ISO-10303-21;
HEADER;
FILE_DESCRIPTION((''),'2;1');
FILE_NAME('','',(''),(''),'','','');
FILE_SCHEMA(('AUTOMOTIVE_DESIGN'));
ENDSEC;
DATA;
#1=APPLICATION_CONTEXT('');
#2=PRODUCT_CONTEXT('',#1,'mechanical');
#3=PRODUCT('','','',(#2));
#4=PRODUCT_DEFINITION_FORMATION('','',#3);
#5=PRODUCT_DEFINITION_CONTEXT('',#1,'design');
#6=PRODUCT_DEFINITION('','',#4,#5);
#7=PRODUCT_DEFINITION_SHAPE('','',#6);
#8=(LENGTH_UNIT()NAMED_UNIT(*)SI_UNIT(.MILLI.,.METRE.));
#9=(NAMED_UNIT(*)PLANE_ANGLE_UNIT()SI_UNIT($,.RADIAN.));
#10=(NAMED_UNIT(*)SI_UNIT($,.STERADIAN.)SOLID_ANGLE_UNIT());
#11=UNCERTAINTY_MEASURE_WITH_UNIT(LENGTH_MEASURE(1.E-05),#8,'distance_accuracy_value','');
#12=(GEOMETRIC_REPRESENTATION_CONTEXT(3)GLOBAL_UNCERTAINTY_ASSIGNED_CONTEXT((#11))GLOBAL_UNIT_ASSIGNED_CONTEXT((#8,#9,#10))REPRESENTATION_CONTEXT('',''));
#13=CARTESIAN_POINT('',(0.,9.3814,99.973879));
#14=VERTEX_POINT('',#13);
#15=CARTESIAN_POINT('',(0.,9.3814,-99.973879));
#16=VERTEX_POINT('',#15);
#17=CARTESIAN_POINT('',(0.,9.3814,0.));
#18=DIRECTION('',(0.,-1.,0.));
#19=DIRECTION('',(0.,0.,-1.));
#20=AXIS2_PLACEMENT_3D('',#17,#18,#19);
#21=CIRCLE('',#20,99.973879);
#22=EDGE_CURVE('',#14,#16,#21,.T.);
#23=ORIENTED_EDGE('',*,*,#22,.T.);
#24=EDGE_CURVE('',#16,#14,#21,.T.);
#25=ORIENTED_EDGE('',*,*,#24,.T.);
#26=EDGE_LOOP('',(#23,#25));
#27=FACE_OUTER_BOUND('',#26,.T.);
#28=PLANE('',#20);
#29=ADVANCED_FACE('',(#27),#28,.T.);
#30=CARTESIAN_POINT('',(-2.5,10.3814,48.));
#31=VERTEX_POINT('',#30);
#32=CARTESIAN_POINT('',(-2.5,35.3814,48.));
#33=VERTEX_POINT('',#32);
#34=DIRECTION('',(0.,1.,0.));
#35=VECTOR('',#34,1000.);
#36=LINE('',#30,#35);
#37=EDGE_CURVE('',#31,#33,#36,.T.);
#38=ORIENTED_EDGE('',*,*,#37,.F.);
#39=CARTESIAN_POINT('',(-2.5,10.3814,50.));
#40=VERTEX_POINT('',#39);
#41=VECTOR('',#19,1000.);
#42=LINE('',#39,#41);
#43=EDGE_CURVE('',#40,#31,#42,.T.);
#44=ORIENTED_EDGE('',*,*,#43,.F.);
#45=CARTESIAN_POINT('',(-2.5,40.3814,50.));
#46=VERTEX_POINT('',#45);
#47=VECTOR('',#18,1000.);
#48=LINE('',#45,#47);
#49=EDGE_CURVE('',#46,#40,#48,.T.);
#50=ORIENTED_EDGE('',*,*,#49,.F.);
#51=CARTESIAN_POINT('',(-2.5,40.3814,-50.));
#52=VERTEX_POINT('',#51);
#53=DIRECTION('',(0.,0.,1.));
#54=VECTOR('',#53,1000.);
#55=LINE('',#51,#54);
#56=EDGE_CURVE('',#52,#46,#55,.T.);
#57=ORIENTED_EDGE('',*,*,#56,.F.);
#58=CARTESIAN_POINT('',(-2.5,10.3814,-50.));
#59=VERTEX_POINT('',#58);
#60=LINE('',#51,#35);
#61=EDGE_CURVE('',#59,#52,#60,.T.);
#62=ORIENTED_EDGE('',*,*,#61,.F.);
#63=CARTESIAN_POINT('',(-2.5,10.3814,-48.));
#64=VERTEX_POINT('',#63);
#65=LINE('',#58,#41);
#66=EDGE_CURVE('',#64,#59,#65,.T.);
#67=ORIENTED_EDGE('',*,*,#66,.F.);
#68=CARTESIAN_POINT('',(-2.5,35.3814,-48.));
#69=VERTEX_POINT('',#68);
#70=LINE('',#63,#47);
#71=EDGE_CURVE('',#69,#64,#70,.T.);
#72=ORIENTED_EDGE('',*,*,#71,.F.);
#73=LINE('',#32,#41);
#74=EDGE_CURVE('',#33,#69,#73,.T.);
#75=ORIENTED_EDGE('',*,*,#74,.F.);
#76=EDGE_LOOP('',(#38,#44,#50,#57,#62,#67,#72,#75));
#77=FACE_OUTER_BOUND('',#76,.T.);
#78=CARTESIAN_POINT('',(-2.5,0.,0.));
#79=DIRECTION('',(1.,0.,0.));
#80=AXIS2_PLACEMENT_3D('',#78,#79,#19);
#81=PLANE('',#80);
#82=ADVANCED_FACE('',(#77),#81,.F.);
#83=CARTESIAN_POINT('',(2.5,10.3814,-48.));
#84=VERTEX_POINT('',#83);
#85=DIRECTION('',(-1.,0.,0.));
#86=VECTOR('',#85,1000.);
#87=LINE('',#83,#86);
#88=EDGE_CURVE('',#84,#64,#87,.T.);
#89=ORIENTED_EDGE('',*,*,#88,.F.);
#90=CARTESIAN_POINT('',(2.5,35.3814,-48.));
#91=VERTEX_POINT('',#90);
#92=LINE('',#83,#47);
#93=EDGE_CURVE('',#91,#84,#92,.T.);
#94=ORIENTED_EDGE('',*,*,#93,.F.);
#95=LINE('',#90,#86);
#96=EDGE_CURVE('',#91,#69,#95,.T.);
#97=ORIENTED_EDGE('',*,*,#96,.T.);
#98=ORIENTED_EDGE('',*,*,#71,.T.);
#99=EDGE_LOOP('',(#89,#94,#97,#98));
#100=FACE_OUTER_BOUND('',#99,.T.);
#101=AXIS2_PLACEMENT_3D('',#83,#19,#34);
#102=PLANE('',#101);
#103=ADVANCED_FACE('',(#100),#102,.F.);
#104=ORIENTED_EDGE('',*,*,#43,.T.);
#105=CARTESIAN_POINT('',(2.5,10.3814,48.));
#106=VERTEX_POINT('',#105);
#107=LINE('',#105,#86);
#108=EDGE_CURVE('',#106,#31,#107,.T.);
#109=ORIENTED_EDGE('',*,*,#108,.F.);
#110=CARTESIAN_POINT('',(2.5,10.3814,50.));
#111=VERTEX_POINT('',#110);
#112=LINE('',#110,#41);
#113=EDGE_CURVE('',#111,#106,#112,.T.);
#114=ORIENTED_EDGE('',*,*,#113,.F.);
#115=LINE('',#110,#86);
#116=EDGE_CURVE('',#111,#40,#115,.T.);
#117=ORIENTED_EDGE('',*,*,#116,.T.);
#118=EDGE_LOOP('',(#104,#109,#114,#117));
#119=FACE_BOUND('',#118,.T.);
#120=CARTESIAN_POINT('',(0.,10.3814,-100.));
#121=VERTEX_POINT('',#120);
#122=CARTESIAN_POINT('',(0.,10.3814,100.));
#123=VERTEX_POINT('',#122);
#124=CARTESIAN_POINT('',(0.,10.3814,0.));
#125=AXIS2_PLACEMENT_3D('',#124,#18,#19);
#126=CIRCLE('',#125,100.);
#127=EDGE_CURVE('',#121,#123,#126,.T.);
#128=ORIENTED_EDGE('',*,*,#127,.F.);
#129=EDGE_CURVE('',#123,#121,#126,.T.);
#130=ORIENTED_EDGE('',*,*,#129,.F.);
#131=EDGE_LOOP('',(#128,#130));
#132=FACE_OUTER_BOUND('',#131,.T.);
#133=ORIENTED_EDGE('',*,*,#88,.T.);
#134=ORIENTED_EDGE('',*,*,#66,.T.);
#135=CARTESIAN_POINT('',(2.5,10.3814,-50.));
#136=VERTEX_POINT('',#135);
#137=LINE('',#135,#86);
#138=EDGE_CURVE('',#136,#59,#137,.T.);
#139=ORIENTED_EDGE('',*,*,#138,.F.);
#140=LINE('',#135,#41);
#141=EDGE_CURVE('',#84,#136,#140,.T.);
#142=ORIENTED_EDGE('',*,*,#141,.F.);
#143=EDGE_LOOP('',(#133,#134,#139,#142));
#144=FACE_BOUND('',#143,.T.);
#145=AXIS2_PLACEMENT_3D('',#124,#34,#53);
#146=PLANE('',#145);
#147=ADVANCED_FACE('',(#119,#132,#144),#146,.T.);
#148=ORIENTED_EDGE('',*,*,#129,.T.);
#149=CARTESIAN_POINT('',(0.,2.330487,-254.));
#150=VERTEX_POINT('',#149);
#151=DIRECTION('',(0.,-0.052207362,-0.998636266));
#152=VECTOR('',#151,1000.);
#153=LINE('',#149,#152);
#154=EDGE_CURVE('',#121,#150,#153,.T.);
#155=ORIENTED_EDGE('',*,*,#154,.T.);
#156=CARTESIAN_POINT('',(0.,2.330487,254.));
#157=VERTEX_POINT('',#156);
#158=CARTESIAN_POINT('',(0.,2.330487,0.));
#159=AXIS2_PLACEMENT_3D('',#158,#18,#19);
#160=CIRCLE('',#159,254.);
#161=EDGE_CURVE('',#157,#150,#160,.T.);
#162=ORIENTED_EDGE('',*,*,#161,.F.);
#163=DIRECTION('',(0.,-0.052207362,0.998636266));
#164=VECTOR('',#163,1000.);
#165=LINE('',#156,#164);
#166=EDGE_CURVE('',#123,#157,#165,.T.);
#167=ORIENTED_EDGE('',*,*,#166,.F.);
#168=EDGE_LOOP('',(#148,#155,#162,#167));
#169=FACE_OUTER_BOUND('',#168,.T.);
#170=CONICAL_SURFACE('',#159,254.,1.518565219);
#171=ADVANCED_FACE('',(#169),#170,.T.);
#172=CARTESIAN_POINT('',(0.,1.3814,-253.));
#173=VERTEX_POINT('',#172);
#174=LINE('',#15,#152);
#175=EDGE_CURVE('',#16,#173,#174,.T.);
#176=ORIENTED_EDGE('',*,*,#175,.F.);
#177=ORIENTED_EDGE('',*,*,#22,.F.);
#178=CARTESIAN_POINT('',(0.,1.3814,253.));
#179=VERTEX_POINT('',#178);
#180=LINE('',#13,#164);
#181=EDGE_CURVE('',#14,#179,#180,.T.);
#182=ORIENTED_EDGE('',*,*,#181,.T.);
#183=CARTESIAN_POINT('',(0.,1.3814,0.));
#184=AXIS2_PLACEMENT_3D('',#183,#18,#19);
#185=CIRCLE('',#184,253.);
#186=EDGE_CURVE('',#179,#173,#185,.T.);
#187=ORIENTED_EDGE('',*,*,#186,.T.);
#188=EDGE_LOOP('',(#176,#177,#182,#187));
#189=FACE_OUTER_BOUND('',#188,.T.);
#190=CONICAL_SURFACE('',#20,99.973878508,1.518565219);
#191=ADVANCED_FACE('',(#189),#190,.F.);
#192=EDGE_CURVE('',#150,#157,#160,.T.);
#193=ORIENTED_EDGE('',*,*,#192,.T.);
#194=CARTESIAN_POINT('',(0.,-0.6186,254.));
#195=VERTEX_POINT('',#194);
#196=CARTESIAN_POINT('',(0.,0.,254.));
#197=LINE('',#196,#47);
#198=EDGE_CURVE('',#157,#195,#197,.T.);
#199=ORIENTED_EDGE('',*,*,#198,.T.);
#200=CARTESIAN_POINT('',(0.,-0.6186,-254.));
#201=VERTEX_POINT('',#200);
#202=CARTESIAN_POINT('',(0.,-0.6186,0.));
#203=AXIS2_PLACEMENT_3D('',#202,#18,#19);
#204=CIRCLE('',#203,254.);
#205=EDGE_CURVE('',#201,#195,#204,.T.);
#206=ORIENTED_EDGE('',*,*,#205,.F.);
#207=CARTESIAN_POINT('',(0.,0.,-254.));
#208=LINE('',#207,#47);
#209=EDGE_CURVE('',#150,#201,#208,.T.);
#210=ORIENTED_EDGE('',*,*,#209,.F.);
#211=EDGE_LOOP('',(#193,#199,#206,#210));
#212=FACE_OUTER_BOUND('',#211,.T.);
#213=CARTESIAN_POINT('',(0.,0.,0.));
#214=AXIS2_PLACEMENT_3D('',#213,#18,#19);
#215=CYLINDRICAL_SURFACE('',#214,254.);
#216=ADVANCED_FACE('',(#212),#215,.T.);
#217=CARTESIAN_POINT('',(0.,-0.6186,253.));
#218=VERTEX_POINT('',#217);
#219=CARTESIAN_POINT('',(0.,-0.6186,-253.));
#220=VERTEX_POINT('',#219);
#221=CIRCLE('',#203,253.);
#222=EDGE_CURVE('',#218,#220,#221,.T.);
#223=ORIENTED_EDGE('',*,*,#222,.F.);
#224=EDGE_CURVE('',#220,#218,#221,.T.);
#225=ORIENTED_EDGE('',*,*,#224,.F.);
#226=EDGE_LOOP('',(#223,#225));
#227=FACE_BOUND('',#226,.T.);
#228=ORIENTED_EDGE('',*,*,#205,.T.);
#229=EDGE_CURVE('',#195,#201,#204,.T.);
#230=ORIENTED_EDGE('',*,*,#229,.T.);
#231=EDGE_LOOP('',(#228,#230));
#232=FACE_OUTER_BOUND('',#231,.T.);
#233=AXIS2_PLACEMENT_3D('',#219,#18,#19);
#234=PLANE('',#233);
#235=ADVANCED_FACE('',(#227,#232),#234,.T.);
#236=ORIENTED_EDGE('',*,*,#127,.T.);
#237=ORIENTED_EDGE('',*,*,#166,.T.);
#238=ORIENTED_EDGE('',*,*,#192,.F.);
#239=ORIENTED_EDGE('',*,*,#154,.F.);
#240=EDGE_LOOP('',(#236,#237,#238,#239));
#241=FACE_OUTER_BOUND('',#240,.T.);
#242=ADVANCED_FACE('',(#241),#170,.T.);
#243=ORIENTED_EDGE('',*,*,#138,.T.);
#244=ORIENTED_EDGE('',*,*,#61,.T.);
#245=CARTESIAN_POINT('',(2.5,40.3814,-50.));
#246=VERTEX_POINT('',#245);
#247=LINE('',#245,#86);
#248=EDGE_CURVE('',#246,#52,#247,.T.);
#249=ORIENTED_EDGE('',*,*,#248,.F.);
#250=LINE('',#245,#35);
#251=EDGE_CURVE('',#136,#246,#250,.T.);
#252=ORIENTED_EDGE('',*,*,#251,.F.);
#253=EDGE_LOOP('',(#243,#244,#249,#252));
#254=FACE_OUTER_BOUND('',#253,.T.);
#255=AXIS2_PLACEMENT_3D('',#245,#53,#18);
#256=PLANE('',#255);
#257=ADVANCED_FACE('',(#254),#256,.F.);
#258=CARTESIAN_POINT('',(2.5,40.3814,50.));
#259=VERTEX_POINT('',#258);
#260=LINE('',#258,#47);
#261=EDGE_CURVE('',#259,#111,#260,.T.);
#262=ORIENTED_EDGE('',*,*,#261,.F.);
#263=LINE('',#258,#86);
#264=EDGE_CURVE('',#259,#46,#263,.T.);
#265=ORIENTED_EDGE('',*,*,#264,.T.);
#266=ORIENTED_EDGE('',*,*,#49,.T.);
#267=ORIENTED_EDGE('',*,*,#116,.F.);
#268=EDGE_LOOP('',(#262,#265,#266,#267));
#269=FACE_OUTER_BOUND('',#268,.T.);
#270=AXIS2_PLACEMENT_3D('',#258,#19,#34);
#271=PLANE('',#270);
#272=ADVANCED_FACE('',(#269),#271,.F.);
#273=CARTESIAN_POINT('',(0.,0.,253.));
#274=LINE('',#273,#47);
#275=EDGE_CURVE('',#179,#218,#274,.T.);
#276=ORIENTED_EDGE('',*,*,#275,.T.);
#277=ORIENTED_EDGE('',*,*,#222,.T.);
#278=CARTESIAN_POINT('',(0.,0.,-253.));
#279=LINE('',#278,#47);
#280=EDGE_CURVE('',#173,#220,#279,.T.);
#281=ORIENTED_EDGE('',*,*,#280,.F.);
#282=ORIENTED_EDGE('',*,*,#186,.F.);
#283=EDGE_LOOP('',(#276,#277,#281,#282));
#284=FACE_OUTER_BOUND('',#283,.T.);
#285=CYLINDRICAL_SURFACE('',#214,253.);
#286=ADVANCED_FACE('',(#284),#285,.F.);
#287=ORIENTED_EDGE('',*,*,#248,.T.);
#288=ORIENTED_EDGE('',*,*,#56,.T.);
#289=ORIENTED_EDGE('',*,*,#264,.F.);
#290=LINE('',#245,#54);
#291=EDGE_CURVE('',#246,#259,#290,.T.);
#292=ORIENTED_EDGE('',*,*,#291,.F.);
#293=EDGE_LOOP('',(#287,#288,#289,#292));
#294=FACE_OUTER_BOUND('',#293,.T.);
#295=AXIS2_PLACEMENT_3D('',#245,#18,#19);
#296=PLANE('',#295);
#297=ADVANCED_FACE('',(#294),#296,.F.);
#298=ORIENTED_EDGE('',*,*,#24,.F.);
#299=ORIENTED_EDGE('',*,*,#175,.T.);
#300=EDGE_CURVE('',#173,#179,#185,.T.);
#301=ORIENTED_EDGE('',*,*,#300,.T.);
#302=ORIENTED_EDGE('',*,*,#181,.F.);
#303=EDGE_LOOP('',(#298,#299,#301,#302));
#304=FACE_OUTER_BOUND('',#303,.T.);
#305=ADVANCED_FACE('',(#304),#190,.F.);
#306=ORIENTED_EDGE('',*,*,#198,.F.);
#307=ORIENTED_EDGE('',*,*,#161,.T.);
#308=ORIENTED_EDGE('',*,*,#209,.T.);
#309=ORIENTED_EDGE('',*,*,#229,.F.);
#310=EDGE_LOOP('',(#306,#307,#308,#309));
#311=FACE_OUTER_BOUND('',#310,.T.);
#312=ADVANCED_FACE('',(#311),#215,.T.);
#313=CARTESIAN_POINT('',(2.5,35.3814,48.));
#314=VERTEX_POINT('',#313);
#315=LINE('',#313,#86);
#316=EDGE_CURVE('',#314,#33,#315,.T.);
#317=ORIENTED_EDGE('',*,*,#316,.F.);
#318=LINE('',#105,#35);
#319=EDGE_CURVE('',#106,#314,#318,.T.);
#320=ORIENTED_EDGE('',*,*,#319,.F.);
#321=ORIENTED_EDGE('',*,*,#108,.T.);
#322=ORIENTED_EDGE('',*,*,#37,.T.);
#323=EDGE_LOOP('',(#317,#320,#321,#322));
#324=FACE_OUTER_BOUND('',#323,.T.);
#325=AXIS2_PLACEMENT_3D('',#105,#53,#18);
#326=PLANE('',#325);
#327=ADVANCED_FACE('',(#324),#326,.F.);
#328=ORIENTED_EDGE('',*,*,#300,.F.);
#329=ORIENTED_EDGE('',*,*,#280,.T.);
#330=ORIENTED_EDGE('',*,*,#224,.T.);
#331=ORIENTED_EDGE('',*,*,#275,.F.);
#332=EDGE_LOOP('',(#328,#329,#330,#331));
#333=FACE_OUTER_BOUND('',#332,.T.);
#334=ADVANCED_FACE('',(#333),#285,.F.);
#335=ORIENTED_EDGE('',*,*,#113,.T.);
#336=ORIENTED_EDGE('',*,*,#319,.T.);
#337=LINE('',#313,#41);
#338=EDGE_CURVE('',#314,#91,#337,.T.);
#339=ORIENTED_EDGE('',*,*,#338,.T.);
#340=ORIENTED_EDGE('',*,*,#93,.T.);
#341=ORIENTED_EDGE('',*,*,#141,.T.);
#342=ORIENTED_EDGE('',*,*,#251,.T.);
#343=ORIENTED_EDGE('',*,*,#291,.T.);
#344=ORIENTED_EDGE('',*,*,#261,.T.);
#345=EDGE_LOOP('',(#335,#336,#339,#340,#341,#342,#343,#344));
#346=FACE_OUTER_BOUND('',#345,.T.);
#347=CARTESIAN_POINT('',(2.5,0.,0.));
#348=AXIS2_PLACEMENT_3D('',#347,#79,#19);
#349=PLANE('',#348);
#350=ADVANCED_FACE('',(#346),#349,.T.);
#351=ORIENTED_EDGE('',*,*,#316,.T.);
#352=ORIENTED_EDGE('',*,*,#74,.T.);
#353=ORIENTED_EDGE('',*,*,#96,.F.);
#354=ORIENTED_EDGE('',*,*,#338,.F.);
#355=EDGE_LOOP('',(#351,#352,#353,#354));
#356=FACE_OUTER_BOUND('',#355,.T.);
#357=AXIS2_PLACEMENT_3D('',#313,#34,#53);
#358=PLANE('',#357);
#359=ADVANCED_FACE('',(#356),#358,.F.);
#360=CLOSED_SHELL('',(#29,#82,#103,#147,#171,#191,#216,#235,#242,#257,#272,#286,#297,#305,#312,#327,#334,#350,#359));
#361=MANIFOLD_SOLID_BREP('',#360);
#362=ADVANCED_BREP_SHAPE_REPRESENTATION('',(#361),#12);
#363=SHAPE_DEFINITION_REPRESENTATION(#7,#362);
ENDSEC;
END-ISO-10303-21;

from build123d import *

# Parameters (mm, degrees)
BOSS_EXTRUDE2_DEPTH = 2.5


with BuildPart() as part:
    # Sketch1 → Revolve1 (revolve)
    with BuildSketch(Plane(origin=(0, 0, 0), x_dir=(0, 0, -1), z_dir=(1, 0, 0))):
        Polygon((253, -0.618600266), (253, 1.381399734), (99.973878508, 9.381399734), (0, 9.381399734), (0, 10.381399734), (100, 10.381399734), (254, 2.330486674), (254, 1.381399734), (254, -0.618600266), align=None)
    revolve(axis=Axis((0, 0, 0), (0, 1, 0)))

    # Sketch2 → Boss-Extrude2 (add, symmetric)
    with BuildSketch(Plane(origin=(0, 0, 0), x_dir=(0, 0, -1), z_dir=(1, 0, 0))):
        Polygon((-48, 10.381399734), (-48, 35.381399734), (48, 35.381399734), (48, 10.381399734), (50, 10.381399734), (50, 40.381399734), (-50, 40.381399734), (-50, 10.381399734), align=None)
    extrude(amount=BOSS_EXTRUDE2_DEPTH, both=True)


solid = part.part
